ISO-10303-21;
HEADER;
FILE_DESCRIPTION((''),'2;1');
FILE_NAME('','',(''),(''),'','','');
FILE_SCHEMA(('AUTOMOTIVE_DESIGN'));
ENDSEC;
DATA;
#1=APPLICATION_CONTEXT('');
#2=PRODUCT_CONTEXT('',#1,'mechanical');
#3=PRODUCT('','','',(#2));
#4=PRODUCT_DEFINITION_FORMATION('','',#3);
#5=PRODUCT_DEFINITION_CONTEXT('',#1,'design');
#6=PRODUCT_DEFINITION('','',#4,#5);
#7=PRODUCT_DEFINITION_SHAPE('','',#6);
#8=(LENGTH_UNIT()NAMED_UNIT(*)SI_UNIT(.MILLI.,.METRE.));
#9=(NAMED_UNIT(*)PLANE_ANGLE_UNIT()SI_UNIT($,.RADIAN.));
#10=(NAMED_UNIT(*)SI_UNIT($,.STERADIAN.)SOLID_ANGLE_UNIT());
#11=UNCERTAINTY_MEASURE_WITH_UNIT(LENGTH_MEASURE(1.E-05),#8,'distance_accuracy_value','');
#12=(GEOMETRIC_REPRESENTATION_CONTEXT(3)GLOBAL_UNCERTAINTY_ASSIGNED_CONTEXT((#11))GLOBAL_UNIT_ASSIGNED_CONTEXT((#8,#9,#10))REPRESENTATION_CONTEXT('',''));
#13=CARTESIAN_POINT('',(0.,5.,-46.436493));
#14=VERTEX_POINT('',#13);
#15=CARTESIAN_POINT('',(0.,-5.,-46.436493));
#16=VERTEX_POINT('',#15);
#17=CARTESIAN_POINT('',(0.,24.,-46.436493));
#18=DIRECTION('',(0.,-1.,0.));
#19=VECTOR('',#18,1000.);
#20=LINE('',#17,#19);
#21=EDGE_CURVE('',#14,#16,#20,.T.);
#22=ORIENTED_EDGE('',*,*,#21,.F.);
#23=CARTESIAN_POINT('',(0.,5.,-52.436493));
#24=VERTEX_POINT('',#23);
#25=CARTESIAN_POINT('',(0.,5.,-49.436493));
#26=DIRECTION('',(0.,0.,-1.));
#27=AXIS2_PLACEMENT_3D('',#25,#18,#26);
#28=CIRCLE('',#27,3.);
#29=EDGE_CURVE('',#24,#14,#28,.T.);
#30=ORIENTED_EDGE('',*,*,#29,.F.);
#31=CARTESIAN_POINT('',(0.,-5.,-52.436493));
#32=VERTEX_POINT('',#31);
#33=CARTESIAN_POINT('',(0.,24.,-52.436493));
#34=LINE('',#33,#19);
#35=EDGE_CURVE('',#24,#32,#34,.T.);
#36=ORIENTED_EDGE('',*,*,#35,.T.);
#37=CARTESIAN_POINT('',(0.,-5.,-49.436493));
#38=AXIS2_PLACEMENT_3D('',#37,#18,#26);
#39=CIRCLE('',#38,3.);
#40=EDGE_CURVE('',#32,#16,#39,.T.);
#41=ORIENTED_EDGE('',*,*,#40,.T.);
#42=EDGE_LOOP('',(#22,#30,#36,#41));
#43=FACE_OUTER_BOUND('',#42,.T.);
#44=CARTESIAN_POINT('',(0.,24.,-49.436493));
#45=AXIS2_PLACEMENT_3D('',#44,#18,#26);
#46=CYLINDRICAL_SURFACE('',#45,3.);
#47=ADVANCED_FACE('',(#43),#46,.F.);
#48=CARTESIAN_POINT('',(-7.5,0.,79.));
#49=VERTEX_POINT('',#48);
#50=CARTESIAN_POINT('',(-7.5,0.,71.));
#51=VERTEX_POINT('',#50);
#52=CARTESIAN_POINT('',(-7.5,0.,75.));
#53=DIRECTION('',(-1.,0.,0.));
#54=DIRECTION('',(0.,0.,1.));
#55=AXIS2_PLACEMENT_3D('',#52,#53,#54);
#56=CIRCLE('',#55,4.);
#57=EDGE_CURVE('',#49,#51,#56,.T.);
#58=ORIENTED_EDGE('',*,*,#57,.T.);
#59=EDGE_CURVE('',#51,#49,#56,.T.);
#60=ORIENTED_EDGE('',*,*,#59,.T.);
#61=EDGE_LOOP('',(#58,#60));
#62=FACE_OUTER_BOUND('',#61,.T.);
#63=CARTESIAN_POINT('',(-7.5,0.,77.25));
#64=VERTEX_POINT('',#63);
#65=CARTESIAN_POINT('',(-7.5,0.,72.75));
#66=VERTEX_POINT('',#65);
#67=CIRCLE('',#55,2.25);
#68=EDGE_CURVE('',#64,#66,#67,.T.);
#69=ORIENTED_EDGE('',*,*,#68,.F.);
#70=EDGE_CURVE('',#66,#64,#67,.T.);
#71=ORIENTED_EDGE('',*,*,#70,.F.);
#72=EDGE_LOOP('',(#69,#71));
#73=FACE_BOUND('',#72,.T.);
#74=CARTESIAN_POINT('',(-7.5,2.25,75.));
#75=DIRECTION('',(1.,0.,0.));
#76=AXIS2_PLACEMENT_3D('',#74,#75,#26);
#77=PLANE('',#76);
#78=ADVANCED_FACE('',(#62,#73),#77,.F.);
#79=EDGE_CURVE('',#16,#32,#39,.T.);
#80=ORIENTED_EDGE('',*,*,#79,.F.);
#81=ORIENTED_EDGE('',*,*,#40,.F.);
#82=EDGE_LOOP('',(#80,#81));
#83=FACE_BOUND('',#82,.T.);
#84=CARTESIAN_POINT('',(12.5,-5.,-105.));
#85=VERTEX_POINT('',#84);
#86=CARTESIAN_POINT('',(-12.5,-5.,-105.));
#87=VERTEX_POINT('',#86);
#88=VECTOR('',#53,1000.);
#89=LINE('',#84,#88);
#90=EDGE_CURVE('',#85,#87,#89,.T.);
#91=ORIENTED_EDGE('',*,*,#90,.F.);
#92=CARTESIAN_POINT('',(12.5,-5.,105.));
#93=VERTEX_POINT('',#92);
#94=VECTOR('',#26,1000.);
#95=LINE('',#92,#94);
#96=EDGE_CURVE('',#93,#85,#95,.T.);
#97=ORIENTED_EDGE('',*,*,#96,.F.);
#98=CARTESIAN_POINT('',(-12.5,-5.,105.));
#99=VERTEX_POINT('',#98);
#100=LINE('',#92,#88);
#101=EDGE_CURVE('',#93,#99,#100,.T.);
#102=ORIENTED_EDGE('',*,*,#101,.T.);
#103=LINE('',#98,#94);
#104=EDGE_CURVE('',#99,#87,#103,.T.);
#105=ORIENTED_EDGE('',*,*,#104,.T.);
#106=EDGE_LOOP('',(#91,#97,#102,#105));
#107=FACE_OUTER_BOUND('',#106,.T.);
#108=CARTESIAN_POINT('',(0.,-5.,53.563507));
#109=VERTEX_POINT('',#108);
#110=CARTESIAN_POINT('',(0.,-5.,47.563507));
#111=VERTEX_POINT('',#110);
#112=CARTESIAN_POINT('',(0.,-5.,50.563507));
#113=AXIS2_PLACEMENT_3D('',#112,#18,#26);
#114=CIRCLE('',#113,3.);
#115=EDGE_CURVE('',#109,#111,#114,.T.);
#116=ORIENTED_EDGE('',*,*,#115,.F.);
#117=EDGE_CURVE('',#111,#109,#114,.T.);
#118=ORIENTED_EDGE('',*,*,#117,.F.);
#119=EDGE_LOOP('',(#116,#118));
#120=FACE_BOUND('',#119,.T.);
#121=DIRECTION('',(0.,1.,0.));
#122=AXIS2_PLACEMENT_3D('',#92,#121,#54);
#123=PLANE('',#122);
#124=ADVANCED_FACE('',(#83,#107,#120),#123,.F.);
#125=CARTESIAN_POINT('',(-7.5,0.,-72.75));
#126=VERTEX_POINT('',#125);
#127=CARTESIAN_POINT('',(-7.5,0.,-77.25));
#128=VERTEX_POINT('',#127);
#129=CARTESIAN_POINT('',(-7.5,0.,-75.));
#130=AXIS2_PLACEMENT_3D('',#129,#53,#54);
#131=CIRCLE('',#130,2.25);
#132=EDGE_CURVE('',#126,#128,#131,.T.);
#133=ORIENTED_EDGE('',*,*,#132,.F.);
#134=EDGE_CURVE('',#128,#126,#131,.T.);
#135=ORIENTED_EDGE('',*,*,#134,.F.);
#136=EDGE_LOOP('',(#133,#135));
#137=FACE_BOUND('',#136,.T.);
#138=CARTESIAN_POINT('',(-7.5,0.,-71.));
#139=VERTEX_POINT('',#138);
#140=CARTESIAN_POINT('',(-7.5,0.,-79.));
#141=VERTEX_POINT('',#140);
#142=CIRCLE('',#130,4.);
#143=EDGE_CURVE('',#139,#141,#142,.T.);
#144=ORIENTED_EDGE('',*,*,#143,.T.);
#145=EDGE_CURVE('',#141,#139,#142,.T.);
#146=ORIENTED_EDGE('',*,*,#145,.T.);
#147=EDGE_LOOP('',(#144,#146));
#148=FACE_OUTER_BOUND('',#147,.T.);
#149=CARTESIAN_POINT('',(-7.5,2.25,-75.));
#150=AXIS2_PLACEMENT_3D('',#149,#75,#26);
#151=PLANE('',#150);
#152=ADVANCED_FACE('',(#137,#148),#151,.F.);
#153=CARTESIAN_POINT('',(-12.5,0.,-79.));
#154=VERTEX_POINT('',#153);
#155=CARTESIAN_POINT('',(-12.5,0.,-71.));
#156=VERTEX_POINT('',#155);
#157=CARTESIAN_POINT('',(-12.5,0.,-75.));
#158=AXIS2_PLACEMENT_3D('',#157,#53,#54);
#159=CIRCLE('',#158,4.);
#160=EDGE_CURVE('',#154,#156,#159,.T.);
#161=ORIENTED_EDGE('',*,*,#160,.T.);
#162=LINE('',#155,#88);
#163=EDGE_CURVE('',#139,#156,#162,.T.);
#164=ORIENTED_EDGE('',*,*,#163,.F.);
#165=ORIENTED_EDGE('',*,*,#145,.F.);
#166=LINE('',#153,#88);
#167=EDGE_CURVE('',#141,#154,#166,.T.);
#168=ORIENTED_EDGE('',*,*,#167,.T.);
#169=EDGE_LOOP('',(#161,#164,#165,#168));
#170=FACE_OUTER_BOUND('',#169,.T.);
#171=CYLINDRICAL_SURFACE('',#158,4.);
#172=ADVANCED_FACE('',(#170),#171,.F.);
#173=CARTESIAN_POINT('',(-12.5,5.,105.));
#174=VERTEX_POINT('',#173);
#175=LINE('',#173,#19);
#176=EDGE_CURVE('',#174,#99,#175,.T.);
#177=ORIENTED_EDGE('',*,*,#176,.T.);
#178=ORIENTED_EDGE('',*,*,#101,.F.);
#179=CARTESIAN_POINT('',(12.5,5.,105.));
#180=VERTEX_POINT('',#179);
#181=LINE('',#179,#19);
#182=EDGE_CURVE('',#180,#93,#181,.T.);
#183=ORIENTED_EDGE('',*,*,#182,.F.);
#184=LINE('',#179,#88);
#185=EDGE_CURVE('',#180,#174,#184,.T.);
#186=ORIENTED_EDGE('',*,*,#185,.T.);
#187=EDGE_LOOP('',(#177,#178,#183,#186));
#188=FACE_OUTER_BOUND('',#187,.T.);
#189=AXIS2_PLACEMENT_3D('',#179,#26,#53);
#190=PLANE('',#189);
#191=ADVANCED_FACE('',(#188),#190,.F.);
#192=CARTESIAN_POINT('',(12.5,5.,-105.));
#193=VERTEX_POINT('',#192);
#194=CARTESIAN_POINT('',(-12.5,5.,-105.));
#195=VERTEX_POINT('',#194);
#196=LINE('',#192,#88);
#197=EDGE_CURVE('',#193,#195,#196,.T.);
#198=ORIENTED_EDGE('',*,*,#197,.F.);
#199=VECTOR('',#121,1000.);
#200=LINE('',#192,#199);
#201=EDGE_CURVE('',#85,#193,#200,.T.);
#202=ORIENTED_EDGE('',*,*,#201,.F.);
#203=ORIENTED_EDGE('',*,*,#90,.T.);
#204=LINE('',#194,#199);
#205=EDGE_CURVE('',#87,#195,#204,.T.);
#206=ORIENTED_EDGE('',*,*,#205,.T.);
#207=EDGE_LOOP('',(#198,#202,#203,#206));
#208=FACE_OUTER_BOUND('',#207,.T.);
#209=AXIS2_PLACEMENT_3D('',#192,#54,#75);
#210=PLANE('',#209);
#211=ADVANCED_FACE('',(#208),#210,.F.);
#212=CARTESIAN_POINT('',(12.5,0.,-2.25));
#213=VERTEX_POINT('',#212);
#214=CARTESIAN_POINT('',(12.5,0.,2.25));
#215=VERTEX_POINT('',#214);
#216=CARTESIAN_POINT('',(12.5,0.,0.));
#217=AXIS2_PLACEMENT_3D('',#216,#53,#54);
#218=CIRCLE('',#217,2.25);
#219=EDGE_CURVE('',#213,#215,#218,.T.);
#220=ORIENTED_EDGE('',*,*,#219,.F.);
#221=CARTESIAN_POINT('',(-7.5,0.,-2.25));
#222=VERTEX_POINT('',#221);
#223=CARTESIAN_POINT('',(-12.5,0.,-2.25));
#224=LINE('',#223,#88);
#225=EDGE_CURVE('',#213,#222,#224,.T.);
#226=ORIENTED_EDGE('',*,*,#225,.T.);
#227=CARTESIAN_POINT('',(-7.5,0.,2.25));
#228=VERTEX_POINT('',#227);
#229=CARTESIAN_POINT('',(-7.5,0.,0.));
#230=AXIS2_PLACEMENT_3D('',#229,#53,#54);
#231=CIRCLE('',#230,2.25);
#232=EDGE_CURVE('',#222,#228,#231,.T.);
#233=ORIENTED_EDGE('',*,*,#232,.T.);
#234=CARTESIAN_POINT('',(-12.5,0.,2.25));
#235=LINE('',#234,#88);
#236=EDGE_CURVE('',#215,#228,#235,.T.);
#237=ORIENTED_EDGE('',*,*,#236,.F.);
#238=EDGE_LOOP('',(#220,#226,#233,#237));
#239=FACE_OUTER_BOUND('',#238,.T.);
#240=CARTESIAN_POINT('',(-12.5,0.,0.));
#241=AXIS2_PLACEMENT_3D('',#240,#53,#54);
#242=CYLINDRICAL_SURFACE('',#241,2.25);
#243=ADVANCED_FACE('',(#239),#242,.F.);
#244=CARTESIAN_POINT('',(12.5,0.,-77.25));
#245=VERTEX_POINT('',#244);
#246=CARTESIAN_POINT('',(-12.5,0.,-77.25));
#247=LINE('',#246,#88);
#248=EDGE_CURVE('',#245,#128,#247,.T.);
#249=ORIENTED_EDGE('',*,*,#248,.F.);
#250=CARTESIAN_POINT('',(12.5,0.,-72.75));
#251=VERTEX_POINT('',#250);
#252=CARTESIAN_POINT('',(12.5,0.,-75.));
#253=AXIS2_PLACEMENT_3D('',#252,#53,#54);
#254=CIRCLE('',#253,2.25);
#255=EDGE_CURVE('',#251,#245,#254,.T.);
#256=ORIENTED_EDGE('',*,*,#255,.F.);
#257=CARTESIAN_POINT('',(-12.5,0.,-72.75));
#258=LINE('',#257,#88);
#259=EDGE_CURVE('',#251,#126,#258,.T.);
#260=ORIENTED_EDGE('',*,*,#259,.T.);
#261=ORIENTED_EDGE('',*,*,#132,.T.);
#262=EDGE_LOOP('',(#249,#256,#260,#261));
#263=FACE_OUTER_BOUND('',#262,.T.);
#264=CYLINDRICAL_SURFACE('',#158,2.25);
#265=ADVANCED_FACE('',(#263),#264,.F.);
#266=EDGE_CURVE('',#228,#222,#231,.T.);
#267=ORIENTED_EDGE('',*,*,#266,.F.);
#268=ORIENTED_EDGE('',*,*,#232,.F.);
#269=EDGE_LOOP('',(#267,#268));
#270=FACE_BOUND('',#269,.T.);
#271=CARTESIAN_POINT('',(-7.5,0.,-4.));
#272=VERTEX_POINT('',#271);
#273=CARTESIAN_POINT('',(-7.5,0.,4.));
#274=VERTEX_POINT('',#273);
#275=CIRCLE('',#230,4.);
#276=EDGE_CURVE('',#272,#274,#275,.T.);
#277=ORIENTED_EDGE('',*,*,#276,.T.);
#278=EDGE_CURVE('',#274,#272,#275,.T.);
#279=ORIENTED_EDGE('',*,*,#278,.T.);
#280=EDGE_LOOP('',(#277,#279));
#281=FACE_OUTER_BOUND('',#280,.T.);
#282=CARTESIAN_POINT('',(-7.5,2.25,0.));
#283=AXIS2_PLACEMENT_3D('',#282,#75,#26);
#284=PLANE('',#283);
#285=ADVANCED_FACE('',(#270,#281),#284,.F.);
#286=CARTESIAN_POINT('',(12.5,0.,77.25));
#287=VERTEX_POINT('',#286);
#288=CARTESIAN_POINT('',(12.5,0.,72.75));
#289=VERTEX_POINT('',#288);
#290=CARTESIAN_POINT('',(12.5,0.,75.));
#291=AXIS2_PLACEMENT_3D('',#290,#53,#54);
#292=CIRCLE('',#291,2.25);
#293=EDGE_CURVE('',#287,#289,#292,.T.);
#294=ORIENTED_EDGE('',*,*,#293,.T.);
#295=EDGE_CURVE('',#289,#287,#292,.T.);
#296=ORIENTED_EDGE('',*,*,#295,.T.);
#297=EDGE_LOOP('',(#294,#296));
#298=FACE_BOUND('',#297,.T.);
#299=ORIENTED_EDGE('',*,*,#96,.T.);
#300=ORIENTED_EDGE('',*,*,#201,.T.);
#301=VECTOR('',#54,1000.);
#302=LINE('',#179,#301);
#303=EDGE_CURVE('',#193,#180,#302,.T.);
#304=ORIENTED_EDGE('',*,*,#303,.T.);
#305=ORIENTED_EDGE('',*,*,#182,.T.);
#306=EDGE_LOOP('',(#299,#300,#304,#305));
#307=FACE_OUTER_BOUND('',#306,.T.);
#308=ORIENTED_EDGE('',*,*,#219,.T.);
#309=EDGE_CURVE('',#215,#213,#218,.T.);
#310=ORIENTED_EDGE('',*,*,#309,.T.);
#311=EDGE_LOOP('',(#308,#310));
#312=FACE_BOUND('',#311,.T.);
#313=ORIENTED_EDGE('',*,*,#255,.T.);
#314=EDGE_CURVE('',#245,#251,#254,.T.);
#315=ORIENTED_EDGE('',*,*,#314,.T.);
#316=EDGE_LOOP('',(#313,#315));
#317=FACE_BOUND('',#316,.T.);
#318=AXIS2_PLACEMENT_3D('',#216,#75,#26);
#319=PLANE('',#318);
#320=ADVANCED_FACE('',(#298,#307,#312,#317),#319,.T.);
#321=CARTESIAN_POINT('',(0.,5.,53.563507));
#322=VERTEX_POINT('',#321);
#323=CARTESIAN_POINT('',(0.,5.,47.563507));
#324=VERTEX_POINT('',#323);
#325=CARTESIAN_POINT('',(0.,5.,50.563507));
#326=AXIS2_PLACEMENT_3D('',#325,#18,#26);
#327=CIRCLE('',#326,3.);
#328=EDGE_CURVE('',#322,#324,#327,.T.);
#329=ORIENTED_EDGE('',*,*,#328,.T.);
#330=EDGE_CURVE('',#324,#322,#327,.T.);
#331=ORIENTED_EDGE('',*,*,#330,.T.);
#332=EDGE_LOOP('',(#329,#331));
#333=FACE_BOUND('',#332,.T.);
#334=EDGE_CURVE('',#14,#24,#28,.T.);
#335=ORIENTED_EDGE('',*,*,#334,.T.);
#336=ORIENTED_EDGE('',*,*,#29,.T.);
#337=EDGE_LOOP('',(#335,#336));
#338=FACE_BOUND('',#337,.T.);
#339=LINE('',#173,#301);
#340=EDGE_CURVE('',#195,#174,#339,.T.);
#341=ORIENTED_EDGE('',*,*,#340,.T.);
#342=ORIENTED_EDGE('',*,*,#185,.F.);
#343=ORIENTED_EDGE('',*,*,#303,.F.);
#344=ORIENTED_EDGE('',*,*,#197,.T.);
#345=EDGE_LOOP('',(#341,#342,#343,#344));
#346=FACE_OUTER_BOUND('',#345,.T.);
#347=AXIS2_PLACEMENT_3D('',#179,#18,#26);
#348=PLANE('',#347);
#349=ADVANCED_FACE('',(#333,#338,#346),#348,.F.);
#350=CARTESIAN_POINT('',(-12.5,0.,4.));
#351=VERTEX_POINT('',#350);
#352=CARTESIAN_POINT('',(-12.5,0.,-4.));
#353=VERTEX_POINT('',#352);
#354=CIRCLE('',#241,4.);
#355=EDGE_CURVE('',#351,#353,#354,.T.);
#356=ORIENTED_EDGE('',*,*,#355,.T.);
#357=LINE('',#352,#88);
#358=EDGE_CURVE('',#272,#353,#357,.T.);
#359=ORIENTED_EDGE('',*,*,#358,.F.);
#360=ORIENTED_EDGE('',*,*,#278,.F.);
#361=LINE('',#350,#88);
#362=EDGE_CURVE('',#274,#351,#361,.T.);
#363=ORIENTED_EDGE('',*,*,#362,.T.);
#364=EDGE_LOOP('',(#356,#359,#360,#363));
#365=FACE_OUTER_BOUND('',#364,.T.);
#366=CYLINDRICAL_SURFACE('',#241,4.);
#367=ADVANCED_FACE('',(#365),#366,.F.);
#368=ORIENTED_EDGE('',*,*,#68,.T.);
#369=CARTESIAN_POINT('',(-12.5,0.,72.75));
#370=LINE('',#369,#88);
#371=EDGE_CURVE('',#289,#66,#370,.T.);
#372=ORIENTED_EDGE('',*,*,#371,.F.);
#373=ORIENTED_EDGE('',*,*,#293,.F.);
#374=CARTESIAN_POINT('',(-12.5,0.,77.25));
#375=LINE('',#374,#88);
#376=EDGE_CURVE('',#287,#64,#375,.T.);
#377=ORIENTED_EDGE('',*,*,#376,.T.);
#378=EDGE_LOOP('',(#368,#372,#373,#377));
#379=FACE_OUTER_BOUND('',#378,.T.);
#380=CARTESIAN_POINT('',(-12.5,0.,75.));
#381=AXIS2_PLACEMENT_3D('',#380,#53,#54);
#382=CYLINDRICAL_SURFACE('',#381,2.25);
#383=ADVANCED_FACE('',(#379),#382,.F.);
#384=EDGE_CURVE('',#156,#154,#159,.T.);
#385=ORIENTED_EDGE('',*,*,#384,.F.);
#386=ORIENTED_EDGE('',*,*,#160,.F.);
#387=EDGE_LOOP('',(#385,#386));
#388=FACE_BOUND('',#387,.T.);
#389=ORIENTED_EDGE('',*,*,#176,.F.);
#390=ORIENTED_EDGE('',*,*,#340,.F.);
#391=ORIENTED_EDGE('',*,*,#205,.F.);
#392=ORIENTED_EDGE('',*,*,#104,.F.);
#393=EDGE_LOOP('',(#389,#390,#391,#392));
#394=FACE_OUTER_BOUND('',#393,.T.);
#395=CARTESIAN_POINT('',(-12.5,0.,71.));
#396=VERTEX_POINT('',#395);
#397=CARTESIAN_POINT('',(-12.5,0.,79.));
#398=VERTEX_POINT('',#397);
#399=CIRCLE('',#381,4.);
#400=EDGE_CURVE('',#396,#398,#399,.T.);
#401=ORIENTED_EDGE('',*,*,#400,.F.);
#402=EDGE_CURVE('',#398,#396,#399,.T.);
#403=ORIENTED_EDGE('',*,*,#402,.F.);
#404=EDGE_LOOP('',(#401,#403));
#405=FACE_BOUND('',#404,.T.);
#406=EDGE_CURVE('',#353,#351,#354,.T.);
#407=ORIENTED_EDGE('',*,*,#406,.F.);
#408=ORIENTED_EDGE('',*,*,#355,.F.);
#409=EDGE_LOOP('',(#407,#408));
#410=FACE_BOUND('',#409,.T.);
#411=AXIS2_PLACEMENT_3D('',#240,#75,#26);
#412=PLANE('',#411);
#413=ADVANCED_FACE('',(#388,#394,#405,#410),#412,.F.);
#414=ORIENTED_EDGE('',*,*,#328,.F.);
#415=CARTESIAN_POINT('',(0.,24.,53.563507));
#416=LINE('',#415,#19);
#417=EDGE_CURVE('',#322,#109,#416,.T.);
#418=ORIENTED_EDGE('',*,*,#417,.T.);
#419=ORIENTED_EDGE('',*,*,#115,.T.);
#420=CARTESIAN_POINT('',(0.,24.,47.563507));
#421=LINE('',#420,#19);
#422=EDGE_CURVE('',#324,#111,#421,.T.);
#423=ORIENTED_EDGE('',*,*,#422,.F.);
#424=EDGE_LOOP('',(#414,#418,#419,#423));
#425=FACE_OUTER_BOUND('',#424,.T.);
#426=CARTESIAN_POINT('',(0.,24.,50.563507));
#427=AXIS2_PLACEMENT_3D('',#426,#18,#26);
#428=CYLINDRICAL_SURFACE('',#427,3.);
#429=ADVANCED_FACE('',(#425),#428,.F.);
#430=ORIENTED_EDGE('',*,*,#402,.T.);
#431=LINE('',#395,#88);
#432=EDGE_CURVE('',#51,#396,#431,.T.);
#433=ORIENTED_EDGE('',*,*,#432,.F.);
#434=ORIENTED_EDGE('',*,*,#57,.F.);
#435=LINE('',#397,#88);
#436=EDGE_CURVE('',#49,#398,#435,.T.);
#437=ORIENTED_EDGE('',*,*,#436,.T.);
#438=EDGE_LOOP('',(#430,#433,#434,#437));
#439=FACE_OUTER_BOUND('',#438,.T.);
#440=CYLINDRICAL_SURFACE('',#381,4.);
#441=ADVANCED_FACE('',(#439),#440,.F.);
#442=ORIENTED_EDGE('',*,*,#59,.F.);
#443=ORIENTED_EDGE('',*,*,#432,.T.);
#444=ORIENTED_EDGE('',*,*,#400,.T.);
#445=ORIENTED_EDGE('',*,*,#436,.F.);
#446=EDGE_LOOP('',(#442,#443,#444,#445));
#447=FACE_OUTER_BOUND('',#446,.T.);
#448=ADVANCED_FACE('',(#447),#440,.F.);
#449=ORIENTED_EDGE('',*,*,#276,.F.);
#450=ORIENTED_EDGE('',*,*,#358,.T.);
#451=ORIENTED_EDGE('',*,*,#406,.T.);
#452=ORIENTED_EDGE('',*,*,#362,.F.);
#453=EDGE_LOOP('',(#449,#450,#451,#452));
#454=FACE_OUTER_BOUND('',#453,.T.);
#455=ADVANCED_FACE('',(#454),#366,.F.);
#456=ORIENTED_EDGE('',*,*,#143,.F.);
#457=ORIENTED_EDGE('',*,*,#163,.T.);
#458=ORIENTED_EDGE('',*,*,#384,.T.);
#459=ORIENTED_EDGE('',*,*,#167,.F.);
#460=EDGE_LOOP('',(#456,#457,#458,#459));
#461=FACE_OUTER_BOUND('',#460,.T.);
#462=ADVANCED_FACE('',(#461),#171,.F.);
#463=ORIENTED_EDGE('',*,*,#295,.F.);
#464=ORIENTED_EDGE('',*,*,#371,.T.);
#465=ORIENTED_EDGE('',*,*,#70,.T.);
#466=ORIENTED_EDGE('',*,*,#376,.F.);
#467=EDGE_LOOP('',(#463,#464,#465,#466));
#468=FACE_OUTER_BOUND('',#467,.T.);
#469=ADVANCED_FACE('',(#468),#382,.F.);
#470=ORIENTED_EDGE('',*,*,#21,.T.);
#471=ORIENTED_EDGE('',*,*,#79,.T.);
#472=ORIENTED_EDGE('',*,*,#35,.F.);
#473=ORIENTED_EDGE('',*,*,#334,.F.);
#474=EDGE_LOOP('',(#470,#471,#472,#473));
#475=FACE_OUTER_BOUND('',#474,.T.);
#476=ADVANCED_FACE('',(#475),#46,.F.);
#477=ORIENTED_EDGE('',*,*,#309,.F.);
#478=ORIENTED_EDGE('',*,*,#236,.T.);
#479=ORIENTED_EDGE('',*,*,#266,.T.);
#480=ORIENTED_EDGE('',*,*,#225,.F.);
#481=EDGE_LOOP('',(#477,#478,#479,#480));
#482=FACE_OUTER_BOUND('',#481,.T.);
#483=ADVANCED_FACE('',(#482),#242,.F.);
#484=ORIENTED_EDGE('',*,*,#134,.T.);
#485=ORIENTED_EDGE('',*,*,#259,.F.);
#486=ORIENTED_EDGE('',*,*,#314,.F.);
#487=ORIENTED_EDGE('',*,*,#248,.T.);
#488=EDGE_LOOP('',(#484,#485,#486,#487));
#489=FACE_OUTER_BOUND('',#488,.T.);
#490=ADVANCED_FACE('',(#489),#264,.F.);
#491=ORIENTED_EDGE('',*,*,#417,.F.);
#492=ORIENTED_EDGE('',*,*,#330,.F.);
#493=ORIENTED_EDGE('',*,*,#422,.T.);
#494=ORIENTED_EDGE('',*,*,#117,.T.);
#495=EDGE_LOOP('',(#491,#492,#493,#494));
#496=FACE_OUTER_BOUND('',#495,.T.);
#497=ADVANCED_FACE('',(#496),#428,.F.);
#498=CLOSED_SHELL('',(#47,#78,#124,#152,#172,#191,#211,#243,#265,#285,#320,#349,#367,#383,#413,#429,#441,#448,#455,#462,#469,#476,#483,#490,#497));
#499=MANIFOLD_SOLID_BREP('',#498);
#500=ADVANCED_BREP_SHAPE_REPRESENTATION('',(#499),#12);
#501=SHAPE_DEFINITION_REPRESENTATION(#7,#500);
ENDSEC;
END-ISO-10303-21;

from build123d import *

# Parameters (mm, degrees)
SKETCH_1_W                = 210
SKETCH_1_H                = 10
EXTRUDE_1_DEPTH           = 12.5
HOLE_WIZARD_1_D           = 4.5
HOLE_WIZARD_1_CBORE_D     = 8
HOLE_WIZARD_1_CBORE_DEPTH = 5
SKETCH_5_R                = 3
CUT_EXTRUDE_1_DEPTH       = 29


with BuildPart() as part:
    # 草图1 → 凸台-拉伸1 (new, symmetric)
    with BuildSketch(Plane(origin=(0, 0, 0), x_dir=(0, 0, -1), z_dir=(1, 0, 0))):
        Rectangle(SKETCH_1_W, SKETCH_1_H)
    extrude(amount=EXTRUDE_1_DEPTH, both=True)

    # 打孔尺寸(%根据)开槽圆柱头螺钉的类型1 (through all)
    with Locations(Plane.ZY.offset(12.5)):
        with Locations((0, 0), (-75, 0), (75, 0)):
            CounterBoreHole(HOLE_WIZARD_1_D / 2, HOLE_WIZARD_1_CBORE_D / 2, HOLE_WIZARD_1_CBORE_DEPTH)

    # 草图5 → 切除-拉伸1 (cut)
    with BuildSketch(Plane.XZ.offset(5)):
        with Locations(Location((0, 50.563507408, 0), (0, 0, 270))):
            Circle(SKETCH_5_R)
        with Locations(Location((0, -49.436492592, 0), (0, 0, 270))):
            Circle(SKETCH_5_R)
    extrude(amount=-CUT_EXTRUDE_1_DEPTH, mode=Mode.SUBTRACT)


solid = part.part
